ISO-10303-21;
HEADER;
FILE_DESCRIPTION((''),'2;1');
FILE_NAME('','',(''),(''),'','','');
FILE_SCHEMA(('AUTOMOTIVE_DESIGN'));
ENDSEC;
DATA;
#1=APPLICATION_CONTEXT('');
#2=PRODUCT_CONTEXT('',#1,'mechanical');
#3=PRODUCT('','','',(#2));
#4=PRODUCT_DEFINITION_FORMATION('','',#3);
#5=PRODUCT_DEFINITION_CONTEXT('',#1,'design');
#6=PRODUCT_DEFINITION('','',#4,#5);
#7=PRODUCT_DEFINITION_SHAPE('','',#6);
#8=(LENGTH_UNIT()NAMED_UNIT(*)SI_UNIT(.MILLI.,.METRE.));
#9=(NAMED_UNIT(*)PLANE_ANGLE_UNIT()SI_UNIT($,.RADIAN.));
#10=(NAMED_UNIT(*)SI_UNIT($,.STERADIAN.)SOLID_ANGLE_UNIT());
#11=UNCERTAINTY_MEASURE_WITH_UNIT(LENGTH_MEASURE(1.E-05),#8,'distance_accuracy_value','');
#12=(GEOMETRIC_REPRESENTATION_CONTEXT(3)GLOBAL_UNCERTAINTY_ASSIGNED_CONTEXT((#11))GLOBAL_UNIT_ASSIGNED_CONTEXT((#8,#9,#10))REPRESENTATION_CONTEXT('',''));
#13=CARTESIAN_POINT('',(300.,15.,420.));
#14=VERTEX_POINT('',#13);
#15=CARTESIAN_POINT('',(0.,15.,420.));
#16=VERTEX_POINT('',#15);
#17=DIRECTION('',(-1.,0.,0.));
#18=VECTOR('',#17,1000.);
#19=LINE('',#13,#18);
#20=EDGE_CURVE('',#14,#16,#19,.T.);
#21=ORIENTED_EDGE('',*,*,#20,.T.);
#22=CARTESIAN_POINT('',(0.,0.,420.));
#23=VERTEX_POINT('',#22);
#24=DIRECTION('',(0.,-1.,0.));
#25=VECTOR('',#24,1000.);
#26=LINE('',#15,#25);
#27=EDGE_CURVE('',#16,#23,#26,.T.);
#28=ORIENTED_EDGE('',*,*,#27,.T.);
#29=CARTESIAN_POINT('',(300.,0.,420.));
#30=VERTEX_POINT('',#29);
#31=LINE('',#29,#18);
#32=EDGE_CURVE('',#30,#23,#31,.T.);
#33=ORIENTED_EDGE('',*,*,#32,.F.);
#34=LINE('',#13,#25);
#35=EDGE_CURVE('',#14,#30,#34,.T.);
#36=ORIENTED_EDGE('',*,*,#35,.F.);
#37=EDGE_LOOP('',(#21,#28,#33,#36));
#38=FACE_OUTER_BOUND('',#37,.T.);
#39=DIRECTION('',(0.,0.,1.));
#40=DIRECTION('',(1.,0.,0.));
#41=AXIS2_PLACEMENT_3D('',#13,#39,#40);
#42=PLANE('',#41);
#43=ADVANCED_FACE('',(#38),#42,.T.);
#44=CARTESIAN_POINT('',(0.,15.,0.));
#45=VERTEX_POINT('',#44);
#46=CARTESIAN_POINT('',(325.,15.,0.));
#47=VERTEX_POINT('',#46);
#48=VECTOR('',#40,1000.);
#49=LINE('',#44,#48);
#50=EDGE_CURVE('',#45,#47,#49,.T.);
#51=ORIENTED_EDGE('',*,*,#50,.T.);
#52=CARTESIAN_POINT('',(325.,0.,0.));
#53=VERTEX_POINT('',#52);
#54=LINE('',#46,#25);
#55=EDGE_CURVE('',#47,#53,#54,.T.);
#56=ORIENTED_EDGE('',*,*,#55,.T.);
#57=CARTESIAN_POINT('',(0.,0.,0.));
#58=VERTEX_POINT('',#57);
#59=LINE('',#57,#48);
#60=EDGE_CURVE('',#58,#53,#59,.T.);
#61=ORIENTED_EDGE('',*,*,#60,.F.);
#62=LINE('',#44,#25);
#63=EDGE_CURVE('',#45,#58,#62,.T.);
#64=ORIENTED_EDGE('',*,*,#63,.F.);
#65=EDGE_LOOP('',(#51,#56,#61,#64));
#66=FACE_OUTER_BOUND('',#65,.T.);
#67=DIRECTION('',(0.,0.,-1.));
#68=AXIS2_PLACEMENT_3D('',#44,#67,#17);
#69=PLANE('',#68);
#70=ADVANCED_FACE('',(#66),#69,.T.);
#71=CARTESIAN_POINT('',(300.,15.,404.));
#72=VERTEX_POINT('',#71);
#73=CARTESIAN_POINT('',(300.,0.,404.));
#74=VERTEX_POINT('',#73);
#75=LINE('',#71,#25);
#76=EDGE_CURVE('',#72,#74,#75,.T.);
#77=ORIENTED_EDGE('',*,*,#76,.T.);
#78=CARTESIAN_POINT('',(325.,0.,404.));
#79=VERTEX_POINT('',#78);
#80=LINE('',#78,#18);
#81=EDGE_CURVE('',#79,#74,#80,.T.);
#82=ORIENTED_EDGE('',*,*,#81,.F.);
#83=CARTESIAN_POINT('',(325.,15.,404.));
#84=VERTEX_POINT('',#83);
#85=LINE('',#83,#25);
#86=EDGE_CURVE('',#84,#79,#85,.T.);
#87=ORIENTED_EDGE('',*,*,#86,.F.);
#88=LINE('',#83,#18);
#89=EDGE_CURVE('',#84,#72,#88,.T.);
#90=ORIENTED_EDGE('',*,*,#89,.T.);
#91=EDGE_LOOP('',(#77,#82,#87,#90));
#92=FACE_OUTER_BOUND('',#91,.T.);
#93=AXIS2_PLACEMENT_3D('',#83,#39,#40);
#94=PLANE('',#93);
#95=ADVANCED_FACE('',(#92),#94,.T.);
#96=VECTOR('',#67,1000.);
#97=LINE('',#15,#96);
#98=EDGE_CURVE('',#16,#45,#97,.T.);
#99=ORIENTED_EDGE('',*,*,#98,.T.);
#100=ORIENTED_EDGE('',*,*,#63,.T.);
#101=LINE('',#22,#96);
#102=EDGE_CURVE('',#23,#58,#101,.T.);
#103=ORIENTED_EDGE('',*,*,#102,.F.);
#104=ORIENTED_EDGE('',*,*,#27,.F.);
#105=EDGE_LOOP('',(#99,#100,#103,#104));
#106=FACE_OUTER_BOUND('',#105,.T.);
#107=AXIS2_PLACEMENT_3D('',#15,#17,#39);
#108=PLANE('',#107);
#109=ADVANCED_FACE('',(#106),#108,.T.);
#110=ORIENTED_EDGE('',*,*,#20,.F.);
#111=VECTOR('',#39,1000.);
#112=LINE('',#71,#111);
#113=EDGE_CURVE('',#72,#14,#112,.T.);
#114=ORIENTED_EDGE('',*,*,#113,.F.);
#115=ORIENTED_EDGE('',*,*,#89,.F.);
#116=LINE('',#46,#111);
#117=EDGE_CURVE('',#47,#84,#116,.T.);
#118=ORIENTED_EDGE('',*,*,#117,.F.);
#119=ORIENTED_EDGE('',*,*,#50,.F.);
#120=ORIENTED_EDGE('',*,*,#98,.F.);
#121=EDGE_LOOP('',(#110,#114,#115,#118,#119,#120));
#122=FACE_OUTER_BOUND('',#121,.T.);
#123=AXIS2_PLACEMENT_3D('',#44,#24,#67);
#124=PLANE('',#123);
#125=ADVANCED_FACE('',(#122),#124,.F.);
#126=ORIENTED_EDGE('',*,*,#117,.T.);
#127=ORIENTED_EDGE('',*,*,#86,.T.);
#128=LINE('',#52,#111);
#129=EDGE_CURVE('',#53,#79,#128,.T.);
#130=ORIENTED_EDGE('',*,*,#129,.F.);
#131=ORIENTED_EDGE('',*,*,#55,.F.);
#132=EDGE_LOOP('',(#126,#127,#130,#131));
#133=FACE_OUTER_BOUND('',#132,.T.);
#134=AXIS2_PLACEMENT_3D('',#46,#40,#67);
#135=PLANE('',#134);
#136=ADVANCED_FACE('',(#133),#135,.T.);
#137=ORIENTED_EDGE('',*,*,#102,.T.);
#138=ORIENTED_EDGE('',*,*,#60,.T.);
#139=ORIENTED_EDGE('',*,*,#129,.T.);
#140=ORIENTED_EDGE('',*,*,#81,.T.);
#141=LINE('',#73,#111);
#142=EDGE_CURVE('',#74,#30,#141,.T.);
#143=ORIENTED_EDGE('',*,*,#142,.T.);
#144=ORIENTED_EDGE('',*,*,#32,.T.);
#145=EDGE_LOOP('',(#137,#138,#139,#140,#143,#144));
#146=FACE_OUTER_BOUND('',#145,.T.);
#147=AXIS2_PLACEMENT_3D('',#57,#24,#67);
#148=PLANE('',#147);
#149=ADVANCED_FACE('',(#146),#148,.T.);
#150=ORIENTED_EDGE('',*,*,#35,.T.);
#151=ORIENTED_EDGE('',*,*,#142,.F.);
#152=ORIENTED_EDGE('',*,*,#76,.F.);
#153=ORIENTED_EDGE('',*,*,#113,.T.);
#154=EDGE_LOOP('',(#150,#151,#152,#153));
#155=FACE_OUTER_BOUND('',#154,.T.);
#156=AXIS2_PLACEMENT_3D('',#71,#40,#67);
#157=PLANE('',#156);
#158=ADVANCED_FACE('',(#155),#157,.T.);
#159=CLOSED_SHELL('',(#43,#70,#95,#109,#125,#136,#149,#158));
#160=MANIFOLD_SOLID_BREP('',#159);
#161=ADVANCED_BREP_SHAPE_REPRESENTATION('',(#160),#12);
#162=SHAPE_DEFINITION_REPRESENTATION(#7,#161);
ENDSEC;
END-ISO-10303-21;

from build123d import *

# Parameters (mm, degrees)
BOSS_EXTRUDE1_DEPTH = 15


with BuildPart() as part:
    # Sketch1 → Boss-Extrude1 (new body)
    with BuildSketch(Plane.XZ):
        Polygon((300, 420), (0, 420), (0, 0), (325, 0), (325, 404), (300, 404), align=None)
    extrude(amount=-BOSS_EXTRUDE1_DEPTH)


solid = part.part
